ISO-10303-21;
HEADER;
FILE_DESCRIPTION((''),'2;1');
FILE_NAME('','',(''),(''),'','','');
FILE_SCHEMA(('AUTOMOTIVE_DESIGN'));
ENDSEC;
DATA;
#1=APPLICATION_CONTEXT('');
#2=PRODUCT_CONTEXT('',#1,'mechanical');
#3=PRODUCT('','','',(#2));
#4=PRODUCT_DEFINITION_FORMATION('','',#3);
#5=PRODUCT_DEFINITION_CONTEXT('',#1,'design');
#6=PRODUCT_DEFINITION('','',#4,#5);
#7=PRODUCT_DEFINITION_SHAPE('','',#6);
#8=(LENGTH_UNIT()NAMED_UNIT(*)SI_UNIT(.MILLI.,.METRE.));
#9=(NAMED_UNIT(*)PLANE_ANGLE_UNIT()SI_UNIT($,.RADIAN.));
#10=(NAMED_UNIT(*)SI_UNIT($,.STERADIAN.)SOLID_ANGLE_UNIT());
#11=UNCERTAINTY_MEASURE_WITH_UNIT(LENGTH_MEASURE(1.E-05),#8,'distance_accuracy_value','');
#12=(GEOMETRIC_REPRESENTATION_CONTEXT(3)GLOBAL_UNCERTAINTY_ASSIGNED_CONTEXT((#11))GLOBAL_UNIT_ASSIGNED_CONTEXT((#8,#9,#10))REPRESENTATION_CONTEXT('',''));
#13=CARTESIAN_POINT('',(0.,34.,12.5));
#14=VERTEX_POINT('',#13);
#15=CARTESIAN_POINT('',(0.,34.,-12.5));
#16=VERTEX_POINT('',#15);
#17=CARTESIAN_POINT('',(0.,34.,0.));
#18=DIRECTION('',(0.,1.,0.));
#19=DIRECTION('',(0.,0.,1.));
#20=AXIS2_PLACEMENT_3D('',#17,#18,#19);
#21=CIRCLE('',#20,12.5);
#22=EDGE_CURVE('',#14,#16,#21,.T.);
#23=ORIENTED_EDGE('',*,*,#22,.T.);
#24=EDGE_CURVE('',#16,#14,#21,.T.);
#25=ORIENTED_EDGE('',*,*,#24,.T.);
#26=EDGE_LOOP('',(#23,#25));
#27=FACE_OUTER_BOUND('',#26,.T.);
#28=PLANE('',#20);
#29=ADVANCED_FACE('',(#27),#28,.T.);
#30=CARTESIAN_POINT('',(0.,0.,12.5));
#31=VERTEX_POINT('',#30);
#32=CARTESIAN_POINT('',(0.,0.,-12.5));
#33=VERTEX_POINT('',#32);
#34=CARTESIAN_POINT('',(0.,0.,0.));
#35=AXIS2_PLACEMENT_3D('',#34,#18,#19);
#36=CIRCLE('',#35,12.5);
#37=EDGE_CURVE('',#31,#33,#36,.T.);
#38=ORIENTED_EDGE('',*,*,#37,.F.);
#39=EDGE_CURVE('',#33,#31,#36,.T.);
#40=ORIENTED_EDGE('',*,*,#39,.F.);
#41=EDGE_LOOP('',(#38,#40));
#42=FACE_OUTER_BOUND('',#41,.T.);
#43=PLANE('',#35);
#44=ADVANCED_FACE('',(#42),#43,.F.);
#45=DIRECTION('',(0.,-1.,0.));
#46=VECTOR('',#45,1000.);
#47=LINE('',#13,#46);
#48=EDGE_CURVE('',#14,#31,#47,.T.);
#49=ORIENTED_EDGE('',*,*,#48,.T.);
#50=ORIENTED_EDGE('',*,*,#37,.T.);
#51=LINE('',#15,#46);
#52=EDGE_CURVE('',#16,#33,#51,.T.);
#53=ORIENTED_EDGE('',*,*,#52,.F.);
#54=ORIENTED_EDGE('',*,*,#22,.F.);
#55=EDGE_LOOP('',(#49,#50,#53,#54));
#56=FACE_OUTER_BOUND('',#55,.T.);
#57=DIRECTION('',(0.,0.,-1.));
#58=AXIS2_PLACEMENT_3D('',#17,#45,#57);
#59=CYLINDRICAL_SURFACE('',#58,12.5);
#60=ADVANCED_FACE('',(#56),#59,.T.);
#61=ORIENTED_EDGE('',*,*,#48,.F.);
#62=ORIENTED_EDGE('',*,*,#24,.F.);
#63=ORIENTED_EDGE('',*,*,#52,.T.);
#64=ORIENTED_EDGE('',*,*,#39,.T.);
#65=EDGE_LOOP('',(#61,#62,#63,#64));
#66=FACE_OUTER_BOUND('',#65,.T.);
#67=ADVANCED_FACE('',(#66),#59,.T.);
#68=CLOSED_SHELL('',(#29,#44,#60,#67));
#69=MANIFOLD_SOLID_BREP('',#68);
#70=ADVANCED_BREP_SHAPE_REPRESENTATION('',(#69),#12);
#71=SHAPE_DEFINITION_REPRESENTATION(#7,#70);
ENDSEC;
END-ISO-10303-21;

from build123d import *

# Parameters (mm, degrees)
SKETCH_1_R      = 12.5
EXTRUDE_1_DEPTH = 34


with BuildPart() as part:
    # 草图1 → 凸台-拉伸1 (new body)
    with BuildSketch(Plane(origin=(0, 0, 0), x_dir=(1, 0, 0), z_dir=(0, 1, 0))):
        with Locations(Location((0, 0, 0), (0, 0, 270))):
            Circle(SKETCH_1_R)
    extrude(amount=EXTRUDE_1_DEPTH)


solid = part.part
